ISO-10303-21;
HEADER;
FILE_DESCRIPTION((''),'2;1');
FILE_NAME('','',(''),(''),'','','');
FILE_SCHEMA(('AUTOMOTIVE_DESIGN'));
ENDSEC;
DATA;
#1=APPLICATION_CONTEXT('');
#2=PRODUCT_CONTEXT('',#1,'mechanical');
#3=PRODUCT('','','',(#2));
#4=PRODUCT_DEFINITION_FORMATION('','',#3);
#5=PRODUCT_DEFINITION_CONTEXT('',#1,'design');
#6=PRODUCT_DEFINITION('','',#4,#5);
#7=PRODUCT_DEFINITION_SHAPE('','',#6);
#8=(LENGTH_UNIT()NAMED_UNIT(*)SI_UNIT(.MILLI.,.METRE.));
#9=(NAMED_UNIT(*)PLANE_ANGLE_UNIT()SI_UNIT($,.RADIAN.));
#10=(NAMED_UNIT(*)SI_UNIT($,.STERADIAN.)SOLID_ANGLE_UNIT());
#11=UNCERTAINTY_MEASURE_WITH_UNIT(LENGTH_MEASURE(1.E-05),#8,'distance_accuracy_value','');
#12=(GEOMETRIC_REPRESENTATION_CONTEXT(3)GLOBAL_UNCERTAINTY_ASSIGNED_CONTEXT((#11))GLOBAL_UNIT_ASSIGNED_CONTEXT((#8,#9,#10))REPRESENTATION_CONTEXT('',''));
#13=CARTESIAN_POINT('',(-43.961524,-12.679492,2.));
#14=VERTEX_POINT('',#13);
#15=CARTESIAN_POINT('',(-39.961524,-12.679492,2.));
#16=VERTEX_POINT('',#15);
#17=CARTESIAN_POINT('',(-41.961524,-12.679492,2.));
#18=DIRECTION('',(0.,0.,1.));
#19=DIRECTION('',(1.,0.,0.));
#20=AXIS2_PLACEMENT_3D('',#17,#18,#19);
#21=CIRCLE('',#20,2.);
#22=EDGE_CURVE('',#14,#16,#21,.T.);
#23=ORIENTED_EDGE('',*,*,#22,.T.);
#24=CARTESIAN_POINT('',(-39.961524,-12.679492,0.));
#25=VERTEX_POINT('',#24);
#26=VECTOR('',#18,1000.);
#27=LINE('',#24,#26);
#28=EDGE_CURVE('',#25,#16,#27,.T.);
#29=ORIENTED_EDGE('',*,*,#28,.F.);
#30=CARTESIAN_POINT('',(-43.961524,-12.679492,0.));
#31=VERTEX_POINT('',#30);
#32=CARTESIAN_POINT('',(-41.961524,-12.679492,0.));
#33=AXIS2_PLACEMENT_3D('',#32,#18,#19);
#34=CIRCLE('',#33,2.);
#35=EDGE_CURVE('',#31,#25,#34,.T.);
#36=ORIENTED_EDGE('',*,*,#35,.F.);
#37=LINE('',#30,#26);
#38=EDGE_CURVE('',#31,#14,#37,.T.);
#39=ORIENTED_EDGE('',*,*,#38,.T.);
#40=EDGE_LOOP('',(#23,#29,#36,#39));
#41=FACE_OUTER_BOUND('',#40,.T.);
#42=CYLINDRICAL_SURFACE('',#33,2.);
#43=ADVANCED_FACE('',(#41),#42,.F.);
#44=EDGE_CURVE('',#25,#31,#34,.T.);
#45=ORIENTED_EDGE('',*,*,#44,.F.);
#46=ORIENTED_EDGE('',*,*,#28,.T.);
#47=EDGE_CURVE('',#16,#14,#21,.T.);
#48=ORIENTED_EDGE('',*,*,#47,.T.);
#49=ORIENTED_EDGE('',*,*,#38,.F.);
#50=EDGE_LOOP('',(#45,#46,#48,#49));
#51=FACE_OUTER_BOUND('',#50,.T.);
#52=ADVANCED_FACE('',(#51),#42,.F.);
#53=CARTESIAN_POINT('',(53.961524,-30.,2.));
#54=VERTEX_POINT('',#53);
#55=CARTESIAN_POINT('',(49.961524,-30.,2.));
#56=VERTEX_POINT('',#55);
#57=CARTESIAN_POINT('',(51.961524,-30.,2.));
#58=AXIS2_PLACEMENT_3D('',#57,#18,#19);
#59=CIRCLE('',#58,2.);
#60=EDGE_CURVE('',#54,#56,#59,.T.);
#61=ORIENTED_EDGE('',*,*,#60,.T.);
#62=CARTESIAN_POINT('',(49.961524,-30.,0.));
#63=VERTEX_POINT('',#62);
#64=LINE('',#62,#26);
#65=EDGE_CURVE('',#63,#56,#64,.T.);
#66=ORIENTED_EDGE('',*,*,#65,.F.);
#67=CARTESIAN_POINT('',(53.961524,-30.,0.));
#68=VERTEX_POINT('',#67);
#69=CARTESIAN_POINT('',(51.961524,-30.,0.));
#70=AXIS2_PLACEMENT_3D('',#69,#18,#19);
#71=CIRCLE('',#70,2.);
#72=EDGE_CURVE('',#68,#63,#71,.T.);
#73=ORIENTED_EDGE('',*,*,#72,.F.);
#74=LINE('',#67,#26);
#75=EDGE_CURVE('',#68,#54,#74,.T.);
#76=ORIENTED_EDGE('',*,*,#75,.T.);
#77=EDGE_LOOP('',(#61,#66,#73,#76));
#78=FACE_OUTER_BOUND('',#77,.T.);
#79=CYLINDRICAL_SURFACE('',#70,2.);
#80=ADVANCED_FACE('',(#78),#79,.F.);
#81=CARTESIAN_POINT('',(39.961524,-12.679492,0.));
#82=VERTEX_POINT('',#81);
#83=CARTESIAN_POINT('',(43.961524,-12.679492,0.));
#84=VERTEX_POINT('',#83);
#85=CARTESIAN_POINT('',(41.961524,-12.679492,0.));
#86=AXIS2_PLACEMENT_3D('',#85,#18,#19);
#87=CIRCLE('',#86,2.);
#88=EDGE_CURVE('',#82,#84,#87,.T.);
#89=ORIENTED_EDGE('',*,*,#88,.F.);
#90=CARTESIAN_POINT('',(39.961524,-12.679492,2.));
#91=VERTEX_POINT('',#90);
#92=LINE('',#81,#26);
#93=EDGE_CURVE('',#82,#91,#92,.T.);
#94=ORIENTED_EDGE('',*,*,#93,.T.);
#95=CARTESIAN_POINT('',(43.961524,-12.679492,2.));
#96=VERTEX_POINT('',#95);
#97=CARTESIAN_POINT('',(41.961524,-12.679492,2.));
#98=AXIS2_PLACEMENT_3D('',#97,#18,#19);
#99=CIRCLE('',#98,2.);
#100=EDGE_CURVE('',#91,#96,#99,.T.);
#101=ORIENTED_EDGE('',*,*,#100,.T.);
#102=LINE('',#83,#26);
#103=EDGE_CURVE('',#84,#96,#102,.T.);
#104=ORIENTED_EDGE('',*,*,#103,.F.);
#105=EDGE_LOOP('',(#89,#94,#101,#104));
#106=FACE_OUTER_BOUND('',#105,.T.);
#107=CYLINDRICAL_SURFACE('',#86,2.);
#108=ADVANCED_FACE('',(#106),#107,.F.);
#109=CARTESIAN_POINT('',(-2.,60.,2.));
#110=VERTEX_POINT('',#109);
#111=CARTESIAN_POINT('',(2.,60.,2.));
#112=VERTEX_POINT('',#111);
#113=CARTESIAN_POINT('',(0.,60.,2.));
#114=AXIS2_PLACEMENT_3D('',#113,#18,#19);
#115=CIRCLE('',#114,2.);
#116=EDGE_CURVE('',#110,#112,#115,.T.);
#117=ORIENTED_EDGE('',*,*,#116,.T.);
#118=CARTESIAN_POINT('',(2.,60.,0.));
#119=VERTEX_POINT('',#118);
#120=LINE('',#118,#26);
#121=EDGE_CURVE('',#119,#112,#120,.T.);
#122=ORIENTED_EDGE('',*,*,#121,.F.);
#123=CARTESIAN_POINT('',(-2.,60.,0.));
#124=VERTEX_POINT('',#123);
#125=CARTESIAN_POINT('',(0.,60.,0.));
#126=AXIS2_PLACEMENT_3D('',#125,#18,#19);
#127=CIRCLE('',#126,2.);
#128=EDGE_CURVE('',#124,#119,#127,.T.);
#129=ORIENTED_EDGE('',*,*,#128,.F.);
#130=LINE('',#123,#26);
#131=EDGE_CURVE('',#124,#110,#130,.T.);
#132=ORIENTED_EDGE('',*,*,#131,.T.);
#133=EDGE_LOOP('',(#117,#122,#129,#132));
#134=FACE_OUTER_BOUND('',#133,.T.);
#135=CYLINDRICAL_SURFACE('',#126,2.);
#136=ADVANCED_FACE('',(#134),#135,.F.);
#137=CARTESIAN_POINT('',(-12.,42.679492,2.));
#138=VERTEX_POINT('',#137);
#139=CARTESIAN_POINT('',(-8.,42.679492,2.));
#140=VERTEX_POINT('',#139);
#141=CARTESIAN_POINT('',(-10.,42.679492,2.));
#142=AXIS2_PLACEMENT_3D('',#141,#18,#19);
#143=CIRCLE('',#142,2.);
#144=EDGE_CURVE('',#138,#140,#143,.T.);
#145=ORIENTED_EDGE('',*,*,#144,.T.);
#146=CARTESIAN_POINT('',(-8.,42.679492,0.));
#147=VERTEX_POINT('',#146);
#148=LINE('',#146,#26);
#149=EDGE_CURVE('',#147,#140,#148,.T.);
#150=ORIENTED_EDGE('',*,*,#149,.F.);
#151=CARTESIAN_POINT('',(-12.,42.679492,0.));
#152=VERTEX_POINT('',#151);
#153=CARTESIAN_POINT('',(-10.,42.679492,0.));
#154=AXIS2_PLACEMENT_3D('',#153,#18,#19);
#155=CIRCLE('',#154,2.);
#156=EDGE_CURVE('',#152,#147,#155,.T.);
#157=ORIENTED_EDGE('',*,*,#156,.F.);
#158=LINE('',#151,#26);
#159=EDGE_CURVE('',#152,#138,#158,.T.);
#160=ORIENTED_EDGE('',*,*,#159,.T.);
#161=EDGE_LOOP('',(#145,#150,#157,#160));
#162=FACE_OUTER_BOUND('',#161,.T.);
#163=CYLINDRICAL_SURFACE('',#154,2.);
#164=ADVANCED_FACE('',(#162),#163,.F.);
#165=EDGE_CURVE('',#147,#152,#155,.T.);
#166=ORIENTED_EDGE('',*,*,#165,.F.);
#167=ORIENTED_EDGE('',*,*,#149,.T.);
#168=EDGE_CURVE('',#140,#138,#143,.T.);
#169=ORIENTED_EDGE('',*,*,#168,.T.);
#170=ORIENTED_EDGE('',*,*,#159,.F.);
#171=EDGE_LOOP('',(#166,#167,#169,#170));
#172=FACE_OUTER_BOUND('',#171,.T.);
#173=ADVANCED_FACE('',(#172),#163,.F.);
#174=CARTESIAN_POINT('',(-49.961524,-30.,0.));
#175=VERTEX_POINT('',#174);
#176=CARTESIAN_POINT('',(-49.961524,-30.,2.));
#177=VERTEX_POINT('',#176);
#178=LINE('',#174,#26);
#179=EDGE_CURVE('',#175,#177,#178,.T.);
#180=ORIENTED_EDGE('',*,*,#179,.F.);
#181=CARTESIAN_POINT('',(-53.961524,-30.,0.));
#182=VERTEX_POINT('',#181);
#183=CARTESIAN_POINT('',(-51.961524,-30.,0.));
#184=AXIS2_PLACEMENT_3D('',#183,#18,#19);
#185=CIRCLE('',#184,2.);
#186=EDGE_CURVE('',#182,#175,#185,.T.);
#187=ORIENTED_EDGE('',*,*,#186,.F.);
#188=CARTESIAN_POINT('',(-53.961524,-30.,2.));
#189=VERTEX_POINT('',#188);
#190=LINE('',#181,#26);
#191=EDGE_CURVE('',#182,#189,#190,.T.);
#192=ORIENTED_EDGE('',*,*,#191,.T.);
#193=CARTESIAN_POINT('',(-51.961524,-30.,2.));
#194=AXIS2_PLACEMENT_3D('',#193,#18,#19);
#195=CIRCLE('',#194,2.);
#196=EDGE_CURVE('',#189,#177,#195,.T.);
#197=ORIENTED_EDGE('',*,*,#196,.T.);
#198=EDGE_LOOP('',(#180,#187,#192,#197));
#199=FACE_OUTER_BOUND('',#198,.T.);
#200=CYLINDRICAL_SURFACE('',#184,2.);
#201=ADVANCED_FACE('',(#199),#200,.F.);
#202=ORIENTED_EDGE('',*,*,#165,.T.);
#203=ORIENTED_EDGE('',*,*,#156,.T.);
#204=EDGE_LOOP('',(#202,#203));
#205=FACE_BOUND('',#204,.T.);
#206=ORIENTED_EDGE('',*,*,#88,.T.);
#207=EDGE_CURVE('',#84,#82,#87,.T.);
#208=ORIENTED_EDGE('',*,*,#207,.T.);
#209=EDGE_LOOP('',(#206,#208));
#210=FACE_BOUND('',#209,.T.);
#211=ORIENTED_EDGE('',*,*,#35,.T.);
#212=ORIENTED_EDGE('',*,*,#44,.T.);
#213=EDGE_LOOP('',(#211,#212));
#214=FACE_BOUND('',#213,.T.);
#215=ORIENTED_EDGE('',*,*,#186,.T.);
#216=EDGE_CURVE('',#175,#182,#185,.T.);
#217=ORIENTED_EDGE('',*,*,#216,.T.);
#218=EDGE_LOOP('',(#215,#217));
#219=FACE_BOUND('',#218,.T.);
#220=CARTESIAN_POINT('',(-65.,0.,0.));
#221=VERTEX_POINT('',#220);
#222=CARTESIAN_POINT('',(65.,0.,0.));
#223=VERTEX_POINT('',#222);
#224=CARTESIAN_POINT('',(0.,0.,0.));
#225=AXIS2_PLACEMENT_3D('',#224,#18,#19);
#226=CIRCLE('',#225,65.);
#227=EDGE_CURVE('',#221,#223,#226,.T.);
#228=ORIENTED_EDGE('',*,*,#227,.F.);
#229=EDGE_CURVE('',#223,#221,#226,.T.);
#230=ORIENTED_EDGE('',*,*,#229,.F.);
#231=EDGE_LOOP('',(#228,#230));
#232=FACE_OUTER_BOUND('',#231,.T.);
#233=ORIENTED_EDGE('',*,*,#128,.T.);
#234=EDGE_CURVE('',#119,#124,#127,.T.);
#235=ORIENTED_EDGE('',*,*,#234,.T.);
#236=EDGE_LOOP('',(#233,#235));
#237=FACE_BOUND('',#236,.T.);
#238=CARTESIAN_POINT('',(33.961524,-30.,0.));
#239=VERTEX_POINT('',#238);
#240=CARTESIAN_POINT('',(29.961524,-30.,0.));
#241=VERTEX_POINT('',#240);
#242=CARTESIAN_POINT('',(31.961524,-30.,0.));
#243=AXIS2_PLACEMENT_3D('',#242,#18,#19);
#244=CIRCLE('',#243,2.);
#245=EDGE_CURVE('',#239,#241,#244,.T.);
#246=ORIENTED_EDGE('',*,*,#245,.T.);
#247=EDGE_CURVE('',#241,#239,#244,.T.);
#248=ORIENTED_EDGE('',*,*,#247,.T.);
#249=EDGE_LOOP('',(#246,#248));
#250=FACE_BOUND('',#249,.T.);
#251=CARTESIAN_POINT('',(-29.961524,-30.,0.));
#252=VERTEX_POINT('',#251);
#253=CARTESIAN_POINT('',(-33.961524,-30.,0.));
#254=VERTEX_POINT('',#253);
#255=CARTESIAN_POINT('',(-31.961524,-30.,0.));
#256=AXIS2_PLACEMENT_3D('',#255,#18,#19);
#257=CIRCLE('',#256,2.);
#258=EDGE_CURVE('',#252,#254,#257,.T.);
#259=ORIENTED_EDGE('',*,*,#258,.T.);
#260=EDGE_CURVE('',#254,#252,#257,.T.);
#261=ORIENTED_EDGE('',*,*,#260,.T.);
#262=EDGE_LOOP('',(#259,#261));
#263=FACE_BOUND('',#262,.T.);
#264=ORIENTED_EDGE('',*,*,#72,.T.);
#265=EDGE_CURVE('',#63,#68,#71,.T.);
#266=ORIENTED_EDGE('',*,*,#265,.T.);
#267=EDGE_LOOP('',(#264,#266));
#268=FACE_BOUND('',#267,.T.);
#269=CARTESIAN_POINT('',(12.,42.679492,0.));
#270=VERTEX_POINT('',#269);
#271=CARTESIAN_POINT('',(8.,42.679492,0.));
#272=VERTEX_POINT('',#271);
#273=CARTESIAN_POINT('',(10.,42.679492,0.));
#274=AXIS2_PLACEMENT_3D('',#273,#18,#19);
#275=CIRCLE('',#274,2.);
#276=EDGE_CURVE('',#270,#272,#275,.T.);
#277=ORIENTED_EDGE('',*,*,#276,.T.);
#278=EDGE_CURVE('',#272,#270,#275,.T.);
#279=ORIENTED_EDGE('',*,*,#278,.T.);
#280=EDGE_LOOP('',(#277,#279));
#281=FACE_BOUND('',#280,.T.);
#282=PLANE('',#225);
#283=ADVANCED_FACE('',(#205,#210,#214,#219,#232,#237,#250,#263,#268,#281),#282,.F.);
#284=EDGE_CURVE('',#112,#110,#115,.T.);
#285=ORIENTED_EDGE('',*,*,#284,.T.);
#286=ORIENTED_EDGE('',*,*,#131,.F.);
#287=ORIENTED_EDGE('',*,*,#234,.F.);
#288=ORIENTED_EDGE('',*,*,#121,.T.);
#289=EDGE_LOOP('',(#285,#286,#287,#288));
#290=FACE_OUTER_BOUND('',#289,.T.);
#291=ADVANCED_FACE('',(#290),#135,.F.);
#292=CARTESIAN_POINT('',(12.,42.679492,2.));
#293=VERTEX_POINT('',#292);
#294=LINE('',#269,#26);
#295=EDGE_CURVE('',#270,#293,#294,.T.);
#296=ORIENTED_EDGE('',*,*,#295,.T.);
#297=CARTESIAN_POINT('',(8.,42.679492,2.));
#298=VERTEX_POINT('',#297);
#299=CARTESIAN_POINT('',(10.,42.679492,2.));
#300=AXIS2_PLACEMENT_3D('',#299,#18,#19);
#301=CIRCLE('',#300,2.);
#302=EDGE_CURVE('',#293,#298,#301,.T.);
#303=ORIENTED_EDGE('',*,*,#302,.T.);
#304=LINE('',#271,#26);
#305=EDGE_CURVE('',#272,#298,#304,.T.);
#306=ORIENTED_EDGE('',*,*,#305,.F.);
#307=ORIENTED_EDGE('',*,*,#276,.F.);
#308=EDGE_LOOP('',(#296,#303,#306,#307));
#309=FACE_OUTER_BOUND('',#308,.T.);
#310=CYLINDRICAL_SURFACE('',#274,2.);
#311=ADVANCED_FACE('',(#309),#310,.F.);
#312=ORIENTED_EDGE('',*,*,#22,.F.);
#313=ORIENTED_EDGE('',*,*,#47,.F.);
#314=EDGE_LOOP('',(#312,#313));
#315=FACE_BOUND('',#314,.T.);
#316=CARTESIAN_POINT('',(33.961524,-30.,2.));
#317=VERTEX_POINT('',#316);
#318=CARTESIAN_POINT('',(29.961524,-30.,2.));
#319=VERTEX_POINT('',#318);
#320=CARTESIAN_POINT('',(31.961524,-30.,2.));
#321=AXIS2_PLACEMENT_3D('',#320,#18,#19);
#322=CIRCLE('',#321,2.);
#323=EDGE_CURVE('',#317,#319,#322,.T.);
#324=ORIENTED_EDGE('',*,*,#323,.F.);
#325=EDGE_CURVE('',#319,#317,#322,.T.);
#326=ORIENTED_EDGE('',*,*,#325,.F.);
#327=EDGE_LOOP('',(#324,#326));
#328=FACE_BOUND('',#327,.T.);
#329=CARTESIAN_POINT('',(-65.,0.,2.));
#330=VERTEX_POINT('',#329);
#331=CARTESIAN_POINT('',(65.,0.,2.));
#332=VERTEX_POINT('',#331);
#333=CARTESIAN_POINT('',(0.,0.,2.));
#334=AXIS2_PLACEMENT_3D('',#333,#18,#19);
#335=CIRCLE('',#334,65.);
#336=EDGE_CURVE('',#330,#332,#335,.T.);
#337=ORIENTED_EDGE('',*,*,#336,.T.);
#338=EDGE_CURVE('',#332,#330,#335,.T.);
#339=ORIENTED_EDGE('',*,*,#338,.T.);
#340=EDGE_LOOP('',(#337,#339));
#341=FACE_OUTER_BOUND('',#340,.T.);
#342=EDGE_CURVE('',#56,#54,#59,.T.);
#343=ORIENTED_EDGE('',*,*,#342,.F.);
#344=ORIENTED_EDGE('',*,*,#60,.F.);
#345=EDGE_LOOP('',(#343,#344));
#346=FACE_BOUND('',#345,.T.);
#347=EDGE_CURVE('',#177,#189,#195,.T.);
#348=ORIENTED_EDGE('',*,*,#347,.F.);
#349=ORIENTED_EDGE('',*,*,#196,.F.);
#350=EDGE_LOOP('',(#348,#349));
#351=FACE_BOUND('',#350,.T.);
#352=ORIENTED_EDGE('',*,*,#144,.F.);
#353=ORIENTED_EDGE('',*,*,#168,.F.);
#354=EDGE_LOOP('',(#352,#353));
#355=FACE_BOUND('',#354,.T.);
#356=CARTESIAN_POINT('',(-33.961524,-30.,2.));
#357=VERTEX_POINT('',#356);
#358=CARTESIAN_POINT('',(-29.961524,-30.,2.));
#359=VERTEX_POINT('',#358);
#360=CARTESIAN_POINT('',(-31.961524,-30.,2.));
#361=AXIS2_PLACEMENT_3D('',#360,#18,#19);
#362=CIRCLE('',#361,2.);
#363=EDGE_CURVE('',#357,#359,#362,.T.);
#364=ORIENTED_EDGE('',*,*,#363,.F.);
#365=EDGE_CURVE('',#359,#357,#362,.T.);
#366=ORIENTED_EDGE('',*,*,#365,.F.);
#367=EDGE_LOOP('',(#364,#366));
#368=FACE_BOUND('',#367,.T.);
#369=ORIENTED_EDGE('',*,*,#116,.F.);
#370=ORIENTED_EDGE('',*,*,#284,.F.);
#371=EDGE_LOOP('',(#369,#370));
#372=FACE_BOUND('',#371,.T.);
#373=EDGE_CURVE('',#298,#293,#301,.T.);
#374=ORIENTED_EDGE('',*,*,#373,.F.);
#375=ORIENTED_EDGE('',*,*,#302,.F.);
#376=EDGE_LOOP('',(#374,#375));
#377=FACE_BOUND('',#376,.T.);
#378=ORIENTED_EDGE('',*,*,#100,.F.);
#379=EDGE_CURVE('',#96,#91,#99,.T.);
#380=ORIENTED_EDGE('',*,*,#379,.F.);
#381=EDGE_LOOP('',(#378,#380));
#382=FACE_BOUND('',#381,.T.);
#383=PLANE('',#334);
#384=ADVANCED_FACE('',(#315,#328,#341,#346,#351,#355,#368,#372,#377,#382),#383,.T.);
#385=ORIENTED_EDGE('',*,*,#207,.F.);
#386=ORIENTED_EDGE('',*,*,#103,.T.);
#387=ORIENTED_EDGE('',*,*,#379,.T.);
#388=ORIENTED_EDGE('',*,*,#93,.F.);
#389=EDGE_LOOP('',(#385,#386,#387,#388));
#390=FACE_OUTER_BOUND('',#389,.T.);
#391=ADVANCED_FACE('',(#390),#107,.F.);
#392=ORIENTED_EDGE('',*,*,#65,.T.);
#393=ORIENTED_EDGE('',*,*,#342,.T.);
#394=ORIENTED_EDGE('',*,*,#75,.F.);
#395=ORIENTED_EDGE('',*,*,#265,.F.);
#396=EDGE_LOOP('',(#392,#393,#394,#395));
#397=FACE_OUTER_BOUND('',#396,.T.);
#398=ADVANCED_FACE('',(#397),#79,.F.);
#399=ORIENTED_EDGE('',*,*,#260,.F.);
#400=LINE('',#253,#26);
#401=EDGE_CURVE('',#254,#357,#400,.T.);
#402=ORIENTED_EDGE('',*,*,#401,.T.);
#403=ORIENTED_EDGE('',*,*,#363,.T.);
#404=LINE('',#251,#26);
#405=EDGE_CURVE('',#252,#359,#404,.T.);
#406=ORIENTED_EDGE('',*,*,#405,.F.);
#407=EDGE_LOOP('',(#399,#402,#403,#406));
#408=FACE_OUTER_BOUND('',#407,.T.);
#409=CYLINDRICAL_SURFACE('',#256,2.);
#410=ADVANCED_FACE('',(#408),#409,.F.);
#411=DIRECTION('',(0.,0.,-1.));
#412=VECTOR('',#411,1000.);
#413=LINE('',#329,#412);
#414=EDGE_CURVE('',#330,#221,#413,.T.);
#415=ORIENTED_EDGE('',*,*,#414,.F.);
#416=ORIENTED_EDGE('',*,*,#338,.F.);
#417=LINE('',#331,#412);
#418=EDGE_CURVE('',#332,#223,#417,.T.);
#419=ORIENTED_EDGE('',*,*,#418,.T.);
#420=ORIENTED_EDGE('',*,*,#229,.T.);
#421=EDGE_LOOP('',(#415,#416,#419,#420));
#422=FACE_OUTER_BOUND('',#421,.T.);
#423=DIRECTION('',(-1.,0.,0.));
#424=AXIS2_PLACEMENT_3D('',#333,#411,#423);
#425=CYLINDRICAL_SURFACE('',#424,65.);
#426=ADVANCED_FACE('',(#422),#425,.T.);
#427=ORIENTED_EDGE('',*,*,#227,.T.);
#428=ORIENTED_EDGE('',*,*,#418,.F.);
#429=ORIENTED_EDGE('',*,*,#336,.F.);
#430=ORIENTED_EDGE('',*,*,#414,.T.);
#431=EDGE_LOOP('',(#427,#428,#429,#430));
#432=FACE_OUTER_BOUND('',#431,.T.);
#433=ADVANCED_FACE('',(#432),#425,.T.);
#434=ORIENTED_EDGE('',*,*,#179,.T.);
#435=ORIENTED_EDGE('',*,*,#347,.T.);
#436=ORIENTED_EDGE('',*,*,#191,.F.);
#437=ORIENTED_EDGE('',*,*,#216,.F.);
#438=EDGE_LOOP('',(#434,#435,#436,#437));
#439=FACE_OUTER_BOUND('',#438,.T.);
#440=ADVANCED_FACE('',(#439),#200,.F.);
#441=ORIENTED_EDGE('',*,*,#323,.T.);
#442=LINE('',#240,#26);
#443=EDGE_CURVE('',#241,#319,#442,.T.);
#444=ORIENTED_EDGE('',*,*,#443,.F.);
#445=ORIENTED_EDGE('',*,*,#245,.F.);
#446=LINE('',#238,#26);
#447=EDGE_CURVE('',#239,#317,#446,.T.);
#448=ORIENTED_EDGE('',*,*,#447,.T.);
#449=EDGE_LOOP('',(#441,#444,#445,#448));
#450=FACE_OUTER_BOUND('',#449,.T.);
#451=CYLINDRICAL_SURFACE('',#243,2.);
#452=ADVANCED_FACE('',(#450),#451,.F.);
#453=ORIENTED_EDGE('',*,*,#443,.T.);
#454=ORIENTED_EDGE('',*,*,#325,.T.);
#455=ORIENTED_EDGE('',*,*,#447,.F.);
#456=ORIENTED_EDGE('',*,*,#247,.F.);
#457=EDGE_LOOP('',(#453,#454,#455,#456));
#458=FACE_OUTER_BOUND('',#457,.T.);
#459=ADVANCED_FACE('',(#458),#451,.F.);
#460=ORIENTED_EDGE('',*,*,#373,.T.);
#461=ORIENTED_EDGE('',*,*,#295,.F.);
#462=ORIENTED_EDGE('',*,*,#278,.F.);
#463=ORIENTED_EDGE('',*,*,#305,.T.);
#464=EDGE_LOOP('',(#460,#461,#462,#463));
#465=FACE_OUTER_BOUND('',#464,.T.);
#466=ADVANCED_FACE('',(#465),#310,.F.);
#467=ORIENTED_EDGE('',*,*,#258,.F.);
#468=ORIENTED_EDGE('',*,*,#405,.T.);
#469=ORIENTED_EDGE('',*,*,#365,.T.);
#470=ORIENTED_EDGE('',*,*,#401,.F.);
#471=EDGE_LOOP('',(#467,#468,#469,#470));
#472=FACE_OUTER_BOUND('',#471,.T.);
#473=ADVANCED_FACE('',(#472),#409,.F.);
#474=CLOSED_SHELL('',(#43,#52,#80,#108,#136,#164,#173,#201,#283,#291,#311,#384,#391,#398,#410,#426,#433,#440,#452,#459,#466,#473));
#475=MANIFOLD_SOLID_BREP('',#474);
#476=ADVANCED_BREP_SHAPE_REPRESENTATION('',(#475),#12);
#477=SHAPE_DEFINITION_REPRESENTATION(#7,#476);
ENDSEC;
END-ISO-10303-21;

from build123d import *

# Parameters (mm, degrees)
SKETCH1_R           = 65
BOSS_EXTRUDE1_DEPTH = 2
SKETCH3_R           = 2
CUT_EXTRUDE1_DEPTH  = 92.945636112


with BuildPart() as part:
    # Sketch1 → Boss-Extrude1 (new body)
    with BuildSketch(Plane.XY):
        Circle(SKETCH1_R)
    extrude(amount=BOSS_EXTRUDE1_DEPTH)

    # Sketch3 → Cut-Extrude1 (cut, through all)
    with BuildSketch(Plane.XY.offset(2)):
        with Locations((0, 60)):
            Circle(SKETCH3_R)
        with Locations((10, 42.679491924)):
            Circle(SKETCH3_R)
        with Locations((-10, 42.679491924)):
            Circle(SKETCH3_R)
        with Locations((31.961524227, -30)):
            Circle(SKETCH3_R)
        with Locations((41.961524227, -12.679491924)):
            Circle(SKETCH3_R)
        with Locations((51.961524227, -30)):
            Circle(SKETCH3_R)
        with Locations((-41.961524227, -12.679491924)):
            Circle(SKETCH3_R)
        with Locations((-31.961524227, -30)):
            Circle(SKETCH3_R)
        with Locations((-51.961524227, -30)):
            Circle(SKETCH3_R)
    extrude(amount=-CUT_EXTRUDE1_DEPTH, mode=Mode.SUBTRACT)


solid = part.part
